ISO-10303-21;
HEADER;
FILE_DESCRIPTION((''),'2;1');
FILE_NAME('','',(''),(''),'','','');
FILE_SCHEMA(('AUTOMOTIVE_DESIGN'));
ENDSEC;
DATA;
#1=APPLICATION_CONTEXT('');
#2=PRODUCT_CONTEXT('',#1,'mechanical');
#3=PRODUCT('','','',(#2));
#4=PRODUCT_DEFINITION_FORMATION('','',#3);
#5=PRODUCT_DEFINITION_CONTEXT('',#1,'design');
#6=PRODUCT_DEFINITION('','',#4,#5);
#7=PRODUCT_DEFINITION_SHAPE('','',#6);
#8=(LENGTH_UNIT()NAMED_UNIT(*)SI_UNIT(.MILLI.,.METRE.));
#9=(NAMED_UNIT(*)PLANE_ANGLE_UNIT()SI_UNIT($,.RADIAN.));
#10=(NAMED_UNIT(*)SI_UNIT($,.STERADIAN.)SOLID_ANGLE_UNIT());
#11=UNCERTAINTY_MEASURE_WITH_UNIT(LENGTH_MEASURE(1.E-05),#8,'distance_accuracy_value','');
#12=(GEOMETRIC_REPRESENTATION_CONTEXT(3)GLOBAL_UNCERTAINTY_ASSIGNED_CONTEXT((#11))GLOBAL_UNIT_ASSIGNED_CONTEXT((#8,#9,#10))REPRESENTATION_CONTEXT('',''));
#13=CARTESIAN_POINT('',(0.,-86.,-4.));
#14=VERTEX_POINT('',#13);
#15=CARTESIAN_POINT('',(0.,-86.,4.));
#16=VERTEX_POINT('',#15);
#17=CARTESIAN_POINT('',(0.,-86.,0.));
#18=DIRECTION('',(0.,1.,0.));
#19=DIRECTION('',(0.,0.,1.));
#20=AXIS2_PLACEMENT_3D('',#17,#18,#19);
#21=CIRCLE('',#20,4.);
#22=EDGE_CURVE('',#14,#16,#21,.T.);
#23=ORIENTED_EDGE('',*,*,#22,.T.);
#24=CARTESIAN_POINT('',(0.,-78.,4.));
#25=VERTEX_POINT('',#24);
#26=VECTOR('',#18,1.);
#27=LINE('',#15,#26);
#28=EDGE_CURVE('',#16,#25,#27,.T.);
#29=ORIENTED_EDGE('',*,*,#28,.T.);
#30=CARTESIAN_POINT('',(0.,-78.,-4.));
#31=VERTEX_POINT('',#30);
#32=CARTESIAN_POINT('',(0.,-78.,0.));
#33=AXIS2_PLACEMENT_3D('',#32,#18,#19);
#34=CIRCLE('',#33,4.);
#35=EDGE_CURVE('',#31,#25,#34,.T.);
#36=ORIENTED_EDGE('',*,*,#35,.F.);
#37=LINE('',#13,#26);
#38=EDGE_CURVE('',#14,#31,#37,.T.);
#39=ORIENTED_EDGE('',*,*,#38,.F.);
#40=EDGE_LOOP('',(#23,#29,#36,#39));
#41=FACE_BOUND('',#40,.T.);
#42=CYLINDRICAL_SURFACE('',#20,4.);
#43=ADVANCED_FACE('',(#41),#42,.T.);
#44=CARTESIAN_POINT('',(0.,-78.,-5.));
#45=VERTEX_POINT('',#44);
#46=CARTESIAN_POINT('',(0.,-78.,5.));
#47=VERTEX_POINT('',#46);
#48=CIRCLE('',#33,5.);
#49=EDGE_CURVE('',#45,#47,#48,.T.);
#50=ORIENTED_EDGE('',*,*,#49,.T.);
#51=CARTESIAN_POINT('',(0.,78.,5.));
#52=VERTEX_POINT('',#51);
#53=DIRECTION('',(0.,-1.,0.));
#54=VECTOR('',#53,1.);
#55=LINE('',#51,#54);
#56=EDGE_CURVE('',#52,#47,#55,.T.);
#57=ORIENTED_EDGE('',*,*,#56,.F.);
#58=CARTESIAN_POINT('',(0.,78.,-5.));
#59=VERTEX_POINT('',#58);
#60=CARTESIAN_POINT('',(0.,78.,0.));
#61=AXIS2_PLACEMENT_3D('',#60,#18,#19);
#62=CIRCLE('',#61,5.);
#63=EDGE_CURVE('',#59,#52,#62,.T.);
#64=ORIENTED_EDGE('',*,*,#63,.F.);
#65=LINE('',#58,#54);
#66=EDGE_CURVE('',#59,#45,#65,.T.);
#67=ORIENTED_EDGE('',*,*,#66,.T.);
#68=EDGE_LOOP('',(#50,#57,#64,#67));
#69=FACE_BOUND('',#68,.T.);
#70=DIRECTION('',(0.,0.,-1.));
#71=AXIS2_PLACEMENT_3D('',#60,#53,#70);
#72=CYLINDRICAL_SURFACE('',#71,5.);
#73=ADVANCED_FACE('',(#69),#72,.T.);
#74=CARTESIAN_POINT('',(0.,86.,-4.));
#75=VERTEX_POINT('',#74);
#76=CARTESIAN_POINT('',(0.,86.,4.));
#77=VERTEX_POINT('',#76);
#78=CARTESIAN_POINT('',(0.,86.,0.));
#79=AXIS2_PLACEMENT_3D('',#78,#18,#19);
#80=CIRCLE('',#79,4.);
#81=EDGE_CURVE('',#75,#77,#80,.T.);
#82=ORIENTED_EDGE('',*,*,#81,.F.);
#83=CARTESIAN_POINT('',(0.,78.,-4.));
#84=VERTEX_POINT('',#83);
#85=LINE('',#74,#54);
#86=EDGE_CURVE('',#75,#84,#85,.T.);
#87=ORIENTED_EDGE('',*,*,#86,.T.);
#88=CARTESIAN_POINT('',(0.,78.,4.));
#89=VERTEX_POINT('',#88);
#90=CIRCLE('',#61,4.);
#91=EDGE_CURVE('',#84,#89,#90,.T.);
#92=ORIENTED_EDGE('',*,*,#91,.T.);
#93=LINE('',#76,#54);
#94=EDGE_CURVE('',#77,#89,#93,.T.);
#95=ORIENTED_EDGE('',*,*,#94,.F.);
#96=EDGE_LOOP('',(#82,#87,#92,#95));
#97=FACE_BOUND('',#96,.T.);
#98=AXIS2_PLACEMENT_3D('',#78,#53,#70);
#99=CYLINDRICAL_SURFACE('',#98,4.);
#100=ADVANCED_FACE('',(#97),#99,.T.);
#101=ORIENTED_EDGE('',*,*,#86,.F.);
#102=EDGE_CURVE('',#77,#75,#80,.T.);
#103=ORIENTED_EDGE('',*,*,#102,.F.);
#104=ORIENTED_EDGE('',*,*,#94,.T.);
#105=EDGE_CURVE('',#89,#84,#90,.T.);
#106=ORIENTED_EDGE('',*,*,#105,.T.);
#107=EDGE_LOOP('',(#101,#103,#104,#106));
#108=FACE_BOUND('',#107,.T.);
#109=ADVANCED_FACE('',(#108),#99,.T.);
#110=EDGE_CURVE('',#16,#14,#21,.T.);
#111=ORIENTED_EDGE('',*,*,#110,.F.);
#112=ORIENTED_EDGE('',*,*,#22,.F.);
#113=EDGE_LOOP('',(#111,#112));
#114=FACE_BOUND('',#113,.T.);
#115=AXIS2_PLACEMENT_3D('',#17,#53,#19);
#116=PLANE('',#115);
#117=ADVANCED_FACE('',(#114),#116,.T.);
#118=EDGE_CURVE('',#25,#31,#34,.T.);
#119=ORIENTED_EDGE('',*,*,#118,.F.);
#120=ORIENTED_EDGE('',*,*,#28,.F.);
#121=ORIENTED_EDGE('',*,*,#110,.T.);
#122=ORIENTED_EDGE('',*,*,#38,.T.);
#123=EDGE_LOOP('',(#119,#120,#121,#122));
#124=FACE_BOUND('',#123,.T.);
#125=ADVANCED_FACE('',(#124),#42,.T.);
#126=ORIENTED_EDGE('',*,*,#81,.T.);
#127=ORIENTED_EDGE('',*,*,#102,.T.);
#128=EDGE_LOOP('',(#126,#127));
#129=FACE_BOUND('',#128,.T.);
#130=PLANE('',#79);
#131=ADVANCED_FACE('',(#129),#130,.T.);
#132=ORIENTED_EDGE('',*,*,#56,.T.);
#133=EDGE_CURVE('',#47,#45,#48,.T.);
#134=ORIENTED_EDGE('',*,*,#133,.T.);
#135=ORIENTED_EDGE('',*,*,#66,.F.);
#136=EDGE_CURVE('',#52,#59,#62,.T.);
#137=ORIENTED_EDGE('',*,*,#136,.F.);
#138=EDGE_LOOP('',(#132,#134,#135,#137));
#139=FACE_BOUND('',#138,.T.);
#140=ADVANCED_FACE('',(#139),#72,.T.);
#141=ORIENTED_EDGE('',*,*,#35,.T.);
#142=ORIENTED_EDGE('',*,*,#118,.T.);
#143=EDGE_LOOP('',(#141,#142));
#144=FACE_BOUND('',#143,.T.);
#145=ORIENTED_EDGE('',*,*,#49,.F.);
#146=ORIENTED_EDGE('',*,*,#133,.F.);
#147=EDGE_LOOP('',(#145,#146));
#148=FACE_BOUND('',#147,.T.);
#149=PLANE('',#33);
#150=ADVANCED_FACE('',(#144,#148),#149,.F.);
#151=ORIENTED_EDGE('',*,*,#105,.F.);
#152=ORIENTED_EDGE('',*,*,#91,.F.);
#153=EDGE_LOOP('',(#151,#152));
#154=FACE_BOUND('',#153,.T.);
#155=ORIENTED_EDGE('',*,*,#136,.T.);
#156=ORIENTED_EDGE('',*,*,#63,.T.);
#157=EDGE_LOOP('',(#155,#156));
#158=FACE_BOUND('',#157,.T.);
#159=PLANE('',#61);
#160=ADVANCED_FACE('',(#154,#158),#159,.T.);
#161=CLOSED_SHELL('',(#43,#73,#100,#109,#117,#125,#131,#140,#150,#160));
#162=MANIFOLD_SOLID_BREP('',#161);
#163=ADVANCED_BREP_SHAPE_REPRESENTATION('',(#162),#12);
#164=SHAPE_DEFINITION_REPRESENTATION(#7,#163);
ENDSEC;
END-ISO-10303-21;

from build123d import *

# Parameters (mm, degrees)
SKETCH1_R           = 5
BOSS_EXTRUDE1_DEPTH = 78
SKETCH2_R           = 4
BOSS_EXTRUDE2_DEPTH = 8


with BuildPart() as part:
    # Sketch1 → Boss-Extrude1 (new, symmetric)
    with BuildSketch(Plane(origin=(0, 0, 0), x_dir=(1, 0, 0), z_dir=(0, 1, 0))):
        with Locations(Location((0, 0, 0), (0, 0, 270))):
            Circle(SKETCH1_R)
    extrude(amount=BOSS_EXTRUDE1_DEPTH, both=True)

    # Sketch2 → Boss-Extrude2 (add)
    with BuildSketch(Plane(origin=(0, 78, 0), x_dir=(1, 0, 0), z_dir=(0, 1, 0))):
        with Locations(Location((0, 0, 0), (0, 0, 270))):
            Circle(SKETCH2_R)
    boss_extrude2 = extrude(amount=BOSS_EXTRUDE2_DEPTH)

    # Mirror1: Boss-Extrude2 across plane
    add(boss_extrude2.mirror(Plane.ZX))


solid = part.part
